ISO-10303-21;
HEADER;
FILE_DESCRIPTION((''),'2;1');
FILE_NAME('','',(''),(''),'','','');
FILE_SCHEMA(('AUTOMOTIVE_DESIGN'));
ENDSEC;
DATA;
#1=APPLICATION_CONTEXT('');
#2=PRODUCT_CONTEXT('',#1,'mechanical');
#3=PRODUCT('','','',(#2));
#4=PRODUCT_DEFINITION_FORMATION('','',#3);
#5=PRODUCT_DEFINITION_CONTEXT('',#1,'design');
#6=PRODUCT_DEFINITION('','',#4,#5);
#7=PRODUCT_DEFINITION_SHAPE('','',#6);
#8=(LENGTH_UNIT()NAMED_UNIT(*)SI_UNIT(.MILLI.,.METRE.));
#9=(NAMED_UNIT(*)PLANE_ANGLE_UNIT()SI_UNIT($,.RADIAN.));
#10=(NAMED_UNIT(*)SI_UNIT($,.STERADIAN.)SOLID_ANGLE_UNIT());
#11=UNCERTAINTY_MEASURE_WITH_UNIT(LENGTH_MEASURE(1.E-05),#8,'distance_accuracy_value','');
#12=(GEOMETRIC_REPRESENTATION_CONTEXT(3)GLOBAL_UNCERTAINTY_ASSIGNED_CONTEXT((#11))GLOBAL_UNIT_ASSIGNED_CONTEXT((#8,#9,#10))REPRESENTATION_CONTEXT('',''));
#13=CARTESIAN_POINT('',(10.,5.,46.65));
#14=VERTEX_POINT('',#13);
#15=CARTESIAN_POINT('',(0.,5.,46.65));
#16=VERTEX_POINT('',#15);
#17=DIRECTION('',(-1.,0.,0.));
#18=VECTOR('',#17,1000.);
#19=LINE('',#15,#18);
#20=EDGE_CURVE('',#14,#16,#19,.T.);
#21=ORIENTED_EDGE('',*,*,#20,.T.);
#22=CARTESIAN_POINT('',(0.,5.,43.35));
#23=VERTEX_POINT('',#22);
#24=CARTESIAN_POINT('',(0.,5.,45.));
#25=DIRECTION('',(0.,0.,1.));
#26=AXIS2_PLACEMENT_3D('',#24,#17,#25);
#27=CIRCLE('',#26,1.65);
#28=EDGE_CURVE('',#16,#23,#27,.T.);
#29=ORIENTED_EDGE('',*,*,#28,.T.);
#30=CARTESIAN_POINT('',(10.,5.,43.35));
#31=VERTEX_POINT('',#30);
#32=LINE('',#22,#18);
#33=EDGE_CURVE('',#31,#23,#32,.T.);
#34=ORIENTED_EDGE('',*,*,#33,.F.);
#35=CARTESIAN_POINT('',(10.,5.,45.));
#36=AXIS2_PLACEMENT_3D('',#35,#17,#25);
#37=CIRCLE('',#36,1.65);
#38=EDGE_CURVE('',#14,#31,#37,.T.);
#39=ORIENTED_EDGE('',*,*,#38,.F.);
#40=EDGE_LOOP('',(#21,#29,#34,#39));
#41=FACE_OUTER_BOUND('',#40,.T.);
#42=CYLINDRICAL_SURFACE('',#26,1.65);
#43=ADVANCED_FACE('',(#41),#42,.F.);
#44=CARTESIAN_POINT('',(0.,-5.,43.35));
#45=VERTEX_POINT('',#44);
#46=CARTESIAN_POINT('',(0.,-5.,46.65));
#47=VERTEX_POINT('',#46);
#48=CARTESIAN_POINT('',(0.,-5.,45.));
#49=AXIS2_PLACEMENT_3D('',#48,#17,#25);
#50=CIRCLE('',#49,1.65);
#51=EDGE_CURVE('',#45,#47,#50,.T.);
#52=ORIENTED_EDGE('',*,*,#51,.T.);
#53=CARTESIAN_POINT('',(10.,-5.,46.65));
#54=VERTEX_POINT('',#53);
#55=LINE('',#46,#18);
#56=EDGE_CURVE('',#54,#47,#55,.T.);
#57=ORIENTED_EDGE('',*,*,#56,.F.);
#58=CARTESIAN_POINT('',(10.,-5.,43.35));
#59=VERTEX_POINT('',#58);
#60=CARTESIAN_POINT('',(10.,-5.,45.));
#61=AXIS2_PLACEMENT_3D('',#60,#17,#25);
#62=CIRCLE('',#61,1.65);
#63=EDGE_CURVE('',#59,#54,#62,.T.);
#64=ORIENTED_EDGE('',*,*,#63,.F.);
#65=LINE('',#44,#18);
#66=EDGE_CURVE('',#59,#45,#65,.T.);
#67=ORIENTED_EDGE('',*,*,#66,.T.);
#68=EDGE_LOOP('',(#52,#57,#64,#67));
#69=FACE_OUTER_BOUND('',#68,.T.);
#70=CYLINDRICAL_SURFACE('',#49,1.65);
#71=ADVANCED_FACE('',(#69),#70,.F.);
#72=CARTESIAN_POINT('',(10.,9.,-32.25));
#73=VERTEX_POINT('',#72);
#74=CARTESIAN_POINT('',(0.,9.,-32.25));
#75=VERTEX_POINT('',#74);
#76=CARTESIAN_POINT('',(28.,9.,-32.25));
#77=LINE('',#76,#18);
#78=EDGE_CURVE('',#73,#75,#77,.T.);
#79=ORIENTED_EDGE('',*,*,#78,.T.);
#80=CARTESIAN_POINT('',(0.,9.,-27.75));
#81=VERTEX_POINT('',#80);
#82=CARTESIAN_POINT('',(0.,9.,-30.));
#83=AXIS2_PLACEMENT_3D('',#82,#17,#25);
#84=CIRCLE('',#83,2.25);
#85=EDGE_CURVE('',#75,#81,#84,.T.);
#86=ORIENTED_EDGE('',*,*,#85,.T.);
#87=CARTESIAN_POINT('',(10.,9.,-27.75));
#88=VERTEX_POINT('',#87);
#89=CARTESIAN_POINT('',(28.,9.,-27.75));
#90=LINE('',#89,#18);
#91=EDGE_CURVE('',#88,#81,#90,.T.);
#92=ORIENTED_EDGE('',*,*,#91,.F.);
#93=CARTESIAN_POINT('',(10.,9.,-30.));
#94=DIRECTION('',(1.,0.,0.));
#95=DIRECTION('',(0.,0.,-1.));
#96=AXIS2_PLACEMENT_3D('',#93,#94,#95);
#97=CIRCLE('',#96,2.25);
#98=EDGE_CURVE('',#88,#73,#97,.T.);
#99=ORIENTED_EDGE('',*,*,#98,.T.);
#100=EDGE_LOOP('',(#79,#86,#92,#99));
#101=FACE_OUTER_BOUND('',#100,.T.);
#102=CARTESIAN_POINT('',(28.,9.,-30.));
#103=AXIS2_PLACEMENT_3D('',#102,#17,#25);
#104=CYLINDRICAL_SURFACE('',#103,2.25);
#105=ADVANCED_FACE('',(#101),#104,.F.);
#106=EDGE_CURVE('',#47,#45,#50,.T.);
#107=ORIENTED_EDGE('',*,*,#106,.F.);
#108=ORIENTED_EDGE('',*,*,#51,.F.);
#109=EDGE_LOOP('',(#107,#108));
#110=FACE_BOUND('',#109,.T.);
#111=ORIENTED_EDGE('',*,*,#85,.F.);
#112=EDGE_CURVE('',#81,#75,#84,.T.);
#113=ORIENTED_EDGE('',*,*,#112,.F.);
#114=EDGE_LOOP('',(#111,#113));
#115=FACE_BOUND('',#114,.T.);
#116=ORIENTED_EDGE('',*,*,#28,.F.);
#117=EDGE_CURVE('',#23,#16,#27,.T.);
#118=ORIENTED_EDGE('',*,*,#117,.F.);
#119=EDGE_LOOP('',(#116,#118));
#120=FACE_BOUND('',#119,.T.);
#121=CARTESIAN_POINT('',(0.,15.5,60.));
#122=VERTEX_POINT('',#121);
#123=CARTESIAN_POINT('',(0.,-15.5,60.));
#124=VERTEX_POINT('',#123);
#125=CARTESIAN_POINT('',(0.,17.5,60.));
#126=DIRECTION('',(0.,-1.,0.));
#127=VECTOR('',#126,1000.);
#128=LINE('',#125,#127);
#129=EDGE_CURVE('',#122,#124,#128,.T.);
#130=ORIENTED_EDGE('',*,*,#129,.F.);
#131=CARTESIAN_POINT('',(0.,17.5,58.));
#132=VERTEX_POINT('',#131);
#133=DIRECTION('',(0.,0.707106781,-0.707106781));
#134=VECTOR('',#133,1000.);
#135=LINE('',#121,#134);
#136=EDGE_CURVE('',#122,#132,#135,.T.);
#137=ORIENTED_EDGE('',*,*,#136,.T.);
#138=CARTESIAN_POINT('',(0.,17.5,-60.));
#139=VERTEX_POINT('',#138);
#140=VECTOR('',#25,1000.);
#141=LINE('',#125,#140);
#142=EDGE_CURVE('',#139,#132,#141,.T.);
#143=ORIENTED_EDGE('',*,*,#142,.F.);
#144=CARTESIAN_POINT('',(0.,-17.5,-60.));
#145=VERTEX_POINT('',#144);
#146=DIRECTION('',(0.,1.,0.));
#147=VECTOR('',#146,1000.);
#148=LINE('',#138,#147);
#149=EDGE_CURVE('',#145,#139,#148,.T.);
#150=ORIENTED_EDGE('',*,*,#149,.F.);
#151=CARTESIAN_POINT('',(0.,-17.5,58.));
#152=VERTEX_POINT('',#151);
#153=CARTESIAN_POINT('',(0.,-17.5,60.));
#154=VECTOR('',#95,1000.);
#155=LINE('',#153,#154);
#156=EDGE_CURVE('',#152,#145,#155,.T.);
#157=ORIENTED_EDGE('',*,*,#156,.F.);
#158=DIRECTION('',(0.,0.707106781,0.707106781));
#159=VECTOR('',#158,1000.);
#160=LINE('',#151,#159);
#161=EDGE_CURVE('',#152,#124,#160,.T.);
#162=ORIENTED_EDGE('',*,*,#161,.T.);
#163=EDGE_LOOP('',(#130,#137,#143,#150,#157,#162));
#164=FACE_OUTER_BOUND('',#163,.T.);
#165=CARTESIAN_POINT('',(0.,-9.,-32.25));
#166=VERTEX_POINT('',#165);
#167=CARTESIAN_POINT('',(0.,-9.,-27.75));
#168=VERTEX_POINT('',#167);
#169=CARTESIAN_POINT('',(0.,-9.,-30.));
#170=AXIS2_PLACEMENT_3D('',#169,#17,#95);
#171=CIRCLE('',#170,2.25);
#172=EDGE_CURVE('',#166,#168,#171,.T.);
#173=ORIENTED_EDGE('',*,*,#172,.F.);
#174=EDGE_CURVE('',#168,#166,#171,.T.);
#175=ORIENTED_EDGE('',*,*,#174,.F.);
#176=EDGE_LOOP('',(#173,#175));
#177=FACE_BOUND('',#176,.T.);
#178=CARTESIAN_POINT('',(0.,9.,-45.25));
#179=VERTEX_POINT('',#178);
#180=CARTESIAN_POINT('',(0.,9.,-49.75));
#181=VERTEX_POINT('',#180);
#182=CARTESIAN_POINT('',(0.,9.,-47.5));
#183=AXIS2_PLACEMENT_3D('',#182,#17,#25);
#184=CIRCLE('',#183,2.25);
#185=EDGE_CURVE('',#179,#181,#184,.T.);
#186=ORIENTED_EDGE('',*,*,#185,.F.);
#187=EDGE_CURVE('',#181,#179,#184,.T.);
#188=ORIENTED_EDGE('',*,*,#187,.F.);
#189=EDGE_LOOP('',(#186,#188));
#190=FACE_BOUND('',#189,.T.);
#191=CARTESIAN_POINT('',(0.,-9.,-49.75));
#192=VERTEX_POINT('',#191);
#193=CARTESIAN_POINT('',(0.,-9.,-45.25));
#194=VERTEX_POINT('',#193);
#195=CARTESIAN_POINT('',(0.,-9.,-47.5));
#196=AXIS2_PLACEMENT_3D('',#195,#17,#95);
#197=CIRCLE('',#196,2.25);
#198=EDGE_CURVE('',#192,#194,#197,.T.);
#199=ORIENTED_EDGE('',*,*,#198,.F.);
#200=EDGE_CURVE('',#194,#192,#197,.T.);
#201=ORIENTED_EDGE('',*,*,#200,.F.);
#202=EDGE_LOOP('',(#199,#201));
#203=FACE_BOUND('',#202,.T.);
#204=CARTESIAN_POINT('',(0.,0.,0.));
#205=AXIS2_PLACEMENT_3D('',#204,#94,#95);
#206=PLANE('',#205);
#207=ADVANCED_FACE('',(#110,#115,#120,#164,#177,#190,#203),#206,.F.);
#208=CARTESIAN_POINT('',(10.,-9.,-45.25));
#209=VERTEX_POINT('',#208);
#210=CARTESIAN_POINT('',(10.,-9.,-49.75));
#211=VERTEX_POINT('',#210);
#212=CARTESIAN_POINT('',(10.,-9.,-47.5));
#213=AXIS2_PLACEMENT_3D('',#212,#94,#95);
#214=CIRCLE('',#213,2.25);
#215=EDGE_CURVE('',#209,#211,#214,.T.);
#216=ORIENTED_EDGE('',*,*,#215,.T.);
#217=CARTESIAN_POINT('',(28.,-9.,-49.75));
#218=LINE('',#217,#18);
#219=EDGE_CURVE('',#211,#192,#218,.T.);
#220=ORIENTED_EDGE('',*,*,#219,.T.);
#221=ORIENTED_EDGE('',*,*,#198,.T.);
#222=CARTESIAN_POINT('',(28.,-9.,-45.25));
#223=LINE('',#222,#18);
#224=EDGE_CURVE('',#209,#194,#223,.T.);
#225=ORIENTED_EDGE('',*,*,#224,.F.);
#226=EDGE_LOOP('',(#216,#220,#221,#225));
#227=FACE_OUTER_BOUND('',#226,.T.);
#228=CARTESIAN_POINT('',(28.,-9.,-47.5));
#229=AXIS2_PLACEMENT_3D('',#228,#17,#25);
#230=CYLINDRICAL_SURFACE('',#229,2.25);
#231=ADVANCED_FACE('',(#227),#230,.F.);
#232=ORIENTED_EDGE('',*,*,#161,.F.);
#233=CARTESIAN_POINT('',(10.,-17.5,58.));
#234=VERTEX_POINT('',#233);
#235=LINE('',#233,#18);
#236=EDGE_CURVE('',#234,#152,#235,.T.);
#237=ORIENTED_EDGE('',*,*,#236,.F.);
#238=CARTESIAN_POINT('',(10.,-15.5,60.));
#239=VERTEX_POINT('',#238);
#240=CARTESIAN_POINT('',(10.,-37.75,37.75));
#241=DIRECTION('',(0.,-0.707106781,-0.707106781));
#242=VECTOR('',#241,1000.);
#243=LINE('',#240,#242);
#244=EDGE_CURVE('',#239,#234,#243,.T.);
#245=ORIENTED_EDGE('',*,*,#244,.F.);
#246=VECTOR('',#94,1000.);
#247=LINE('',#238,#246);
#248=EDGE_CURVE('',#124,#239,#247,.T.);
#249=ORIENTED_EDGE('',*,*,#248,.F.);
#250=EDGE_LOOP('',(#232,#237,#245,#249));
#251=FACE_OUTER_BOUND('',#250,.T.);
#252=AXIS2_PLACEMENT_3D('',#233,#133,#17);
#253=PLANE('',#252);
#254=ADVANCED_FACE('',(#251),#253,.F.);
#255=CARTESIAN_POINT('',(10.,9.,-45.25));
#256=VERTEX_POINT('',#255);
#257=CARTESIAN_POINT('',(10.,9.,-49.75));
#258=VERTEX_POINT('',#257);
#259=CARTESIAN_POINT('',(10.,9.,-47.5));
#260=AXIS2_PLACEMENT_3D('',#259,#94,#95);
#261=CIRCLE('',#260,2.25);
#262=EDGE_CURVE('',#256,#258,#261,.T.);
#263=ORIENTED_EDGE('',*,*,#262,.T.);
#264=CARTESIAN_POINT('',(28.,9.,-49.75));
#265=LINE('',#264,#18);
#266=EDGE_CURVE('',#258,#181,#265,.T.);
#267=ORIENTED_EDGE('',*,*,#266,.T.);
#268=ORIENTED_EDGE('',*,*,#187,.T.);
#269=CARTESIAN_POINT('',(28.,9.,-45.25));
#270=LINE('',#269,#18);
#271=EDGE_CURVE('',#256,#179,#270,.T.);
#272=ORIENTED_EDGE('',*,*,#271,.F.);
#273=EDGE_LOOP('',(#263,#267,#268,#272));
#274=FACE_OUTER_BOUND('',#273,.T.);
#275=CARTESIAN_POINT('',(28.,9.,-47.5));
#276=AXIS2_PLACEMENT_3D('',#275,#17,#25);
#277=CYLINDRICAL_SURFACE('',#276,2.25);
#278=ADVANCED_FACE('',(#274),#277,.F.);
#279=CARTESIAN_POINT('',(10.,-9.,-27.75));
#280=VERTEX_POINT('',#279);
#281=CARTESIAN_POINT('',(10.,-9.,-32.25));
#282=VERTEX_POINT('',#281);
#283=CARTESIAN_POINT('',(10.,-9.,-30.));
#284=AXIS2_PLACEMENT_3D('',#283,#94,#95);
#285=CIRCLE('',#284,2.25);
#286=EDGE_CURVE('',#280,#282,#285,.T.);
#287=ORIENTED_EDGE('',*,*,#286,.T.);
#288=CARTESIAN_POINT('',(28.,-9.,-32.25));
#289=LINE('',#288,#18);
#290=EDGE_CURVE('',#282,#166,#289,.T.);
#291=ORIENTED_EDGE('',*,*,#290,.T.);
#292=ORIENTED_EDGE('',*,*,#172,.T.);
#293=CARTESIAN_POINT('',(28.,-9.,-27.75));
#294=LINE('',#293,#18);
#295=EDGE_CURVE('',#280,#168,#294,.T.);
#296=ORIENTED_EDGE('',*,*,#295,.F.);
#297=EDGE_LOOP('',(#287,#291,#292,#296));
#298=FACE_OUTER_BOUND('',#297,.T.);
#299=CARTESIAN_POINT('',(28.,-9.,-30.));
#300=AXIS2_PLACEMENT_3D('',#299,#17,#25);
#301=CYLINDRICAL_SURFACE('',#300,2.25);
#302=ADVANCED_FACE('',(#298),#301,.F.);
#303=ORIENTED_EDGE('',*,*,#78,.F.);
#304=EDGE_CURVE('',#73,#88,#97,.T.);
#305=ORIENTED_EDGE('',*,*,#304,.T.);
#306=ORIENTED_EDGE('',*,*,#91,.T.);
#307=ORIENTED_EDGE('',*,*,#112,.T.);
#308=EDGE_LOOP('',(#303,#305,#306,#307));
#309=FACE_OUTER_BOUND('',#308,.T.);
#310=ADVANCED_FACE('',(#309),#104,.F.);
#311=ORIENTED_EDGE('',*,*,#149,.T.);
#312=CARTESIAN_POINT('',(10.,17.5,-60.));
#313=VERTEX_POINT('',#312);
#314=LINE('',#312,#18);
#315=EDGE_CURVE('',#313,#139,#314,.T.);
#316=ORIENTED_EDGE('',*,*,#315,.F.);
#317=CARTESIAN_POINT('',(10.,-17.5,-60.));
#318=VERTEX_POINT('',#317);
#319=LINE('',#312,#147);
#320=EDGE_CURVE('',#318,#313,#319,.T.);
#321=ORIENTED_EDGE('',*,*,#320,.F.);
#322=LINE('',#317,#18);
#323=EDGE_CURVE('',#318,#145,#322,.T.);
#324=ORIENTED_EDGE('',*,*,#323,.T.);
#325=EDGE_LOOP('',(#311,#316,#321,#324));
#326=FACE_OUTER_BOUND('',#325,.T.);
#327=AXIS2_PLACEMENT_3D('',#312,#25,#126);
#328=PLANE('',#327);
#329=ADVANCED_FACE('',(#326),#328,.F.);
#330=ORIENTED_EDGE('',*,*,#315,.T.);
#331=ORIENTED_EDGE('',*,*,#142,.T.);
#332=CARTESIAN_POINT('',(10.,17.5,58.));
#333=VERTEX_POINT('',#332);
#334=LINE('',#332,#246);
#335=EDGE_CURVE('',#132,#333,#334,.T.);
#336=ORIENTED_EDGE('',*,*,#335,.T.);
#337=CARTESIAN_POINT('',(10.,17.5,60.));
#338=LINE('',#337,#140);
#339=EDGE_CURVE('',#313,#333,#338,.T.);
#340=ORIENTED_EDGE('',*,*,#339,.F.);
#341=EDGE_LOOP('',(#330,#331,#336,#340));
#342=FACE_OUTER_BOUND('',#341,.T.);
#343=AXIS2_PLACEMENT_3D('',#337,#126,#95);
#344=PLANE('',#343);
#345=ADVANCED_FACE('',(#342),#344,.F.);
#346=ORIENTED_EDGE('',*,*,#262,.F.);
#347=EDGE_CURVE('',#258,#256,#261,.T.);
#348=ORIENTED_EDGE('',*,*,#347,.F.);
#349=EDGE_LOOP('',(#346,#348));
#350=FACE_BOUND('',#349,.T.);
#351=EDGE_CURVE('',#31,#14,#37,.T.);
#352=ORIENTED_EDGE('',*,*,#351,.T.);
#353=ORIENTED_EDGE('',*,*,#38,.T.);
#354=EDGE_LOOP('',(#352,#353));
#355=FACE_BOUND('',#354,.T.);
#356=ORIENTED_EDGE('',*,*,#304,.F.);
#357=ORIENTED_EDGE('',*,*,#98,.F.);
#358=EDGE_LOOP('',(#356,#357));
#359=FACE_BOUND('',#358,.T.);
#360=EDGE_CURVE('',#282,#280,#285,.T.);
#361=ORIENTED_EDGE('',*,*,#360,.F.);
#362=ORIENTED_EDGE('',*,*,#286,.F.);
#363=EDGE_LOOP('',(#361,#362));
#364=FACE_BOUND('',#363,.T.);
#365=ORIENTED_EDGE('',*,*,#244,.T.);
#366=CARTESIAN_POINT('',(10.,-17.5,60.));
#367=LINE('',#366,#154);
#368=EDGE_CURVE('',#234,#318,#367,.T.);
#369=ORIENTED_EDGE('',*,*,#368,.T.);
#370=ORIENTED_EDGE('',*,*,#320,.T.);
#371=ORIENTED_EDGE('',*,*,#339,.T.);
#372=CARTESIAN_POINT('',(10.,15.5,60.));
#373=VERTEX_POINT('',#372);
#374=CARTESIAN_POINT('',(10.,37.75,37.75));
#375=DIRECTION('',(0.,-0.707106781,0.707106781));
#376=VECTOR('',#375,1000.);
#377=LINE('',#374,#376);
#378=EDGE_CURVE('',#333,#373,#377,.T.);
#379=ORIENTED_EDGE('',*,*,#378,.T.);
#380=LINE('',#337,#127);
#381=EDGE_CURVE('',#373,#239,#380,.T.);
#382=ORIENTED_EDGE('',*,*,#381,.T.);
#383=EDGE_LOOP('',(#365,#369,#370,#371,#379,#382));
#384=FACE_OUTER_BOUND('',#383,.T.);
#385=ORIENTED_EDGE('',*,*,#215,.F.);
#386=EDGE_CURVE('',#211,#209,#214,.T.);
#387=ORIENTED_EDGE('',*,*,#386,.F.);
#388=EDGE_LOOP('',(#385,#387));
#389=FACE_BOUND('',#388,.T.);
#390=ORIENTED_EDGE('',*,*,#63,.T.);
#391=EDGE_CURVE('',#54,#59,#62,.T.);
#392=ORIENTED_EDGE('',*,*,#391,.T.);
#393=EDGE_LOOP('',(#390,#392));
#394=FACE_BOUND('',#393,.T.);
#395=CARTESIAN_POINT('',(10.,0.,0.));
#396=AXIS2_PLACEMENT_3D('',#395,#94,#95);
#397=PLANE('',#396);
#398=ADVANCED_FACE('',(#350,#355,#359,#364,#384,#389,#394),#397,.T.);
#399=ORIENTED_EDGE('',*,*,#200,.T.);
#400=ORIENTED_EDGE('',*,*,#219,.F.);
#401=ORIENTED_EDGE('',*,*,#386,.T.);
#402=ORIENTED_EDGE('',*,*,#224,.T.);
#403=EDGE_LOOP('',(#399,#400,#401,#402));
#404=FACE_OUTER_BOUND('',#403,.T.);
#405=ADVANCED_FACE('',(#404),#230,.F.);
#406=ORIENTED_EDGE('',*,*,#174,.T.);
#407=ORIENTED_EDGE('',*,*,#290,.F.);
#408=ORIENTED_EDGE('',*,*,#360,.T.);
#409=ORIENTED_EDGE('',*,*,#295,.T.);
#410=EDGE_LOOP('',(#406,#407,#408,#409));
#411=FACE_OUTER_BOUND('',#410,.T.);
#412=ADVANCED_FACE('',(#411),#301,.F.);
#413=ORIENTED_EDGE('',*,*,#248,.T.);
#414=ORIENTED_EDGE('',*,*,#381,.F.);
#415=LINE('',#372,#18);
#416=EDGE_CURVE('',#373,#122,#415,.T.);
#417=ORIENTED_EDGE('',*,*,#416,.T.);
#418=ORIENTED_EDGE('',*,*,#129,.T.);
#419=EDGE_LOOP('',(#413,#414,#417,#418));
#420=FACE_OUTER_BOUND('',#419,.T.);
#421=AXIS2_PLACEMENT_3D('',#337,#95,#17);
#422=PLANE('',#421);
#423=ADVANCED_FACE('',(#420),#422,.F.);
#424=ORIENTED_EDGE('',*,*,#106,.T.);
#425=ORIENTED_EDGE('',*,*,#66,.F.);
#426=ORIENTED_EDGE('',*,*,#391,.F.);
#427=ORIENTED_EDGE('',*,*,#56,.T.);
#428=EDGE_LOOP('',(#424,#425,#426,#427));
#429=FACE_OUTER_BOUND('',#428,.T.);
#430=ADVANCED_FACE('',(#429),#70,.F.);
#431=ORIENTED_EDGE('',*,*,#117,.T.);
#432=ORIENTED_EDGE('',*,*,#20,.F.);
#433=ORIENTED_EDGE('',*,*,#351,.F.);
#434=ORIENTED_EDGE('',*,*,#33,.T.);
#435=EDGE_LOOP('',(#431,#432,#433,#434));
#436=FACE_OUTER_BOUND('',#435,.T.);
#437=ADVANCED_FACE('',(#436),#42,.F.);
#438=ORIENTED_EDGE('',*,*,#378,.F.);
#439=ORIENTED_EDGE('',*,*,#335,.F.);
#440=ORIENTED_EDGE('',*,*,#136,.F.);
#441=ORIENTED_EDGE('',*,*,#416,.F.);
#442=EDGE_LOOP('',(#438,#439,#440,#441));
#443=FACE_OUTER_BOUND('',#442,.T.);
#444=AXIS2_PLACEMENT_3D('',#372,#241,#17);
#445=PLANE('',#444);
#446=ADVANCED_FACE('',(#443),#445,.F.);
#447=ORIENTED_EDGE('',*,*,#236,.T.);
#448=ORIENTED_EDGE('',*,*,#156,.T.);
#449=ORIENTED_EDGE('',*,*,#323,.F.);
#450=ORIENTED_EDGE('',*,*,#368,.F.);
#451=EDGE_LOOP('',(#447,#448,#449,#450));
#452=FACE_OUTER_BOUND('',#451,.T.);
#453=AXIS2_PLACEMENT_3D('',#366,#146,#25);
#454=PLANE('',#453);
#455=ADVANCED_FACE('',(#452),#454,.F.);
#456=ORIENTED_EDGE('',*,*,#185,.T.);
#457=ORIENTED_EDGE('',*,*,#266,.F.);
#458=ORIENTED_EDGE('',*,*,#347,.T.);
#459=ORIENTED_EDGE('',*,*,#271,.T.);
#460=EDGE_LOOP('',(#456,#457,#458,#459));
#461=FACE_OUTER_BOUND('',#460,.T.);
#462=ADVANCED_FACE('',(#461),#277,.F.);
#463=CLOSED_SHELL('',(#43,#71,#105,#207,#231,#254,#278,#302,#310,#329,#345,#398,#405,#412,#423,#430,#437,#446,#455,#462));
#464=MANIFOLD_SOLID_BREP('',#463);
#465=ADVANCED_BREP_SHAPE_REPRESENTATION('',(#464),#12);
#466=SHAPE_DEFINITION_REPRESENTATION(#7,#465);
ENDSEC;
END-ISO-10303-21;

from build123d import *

# Parameters (mm, degrees)
SKETCH_1_W             = 120
SKETCH_1_H             = 35
EXTRUDE_1_DEPTH        = 10
HOLE_WIZARD_M4_1_D     = 3.3
SKETCH_5_R             = 2.25
CUT_EXTRUDE_1_DEPTH    = 28
CHAMFER_1_SIZE         = 2
PATTERN_LINEAR_1_COUNT = 2
PATTERN_LINEAR_1_PITCH = 17.5


with BuildPart() as part:
    # 草图1 → 凸台-拉伸1 (new body)
    with BuildSketch(Plane(origin=(0, 0, 0), x_dir=(0, 0, -1), z_dir=(1, 0, 0))):
        Rectangle(SKETCH_1_W, SKETCH_1_H)
    extrude(amount=EXTRUDE_1_DEPTH)

    # M4 螺纹孔1 (through all)
    with Locations(Plane.ZY):
        with Locations((45, 5), (45, -5)):
            Hole(HOLE_WIZARD_M4_1_D / 2)

    # 草图5 → 切除-拉伸1 (cut)
    with BuildSketch(Plane.ZY):
        with Locations((-47.5, 9)):
            Circle(SKETCH_5_R)
        with Locations(Location((-47.5, -9, 0), (0, 0, 180))):
            Circle(SKETCH_5_R)
    cut_extrude_1 = extrude(amount=-CUT_EXTRUDE_1_DEPTH, mode=Mode.SUBTRACT)

    # 倒角1
    chamfer_1_edges = [part.edges().sort_by_distance(p)[0] for p in [
        (5, -17.5, 60),
        (5, 17.5, 60),
    ]]
    chamfer(chamfer_1_edges, length=CHAMFER_1_SIZE)

    # 阵列(线性)1: 切除-拉伸1 ×2
    with Locations(*[(0, 0, i * PATTERN_LINEAR_1_PITCH) for i in range(1, PATTERN_LINEAR_1_COUNT)]):
        add(cut_extrude_1, mode=Mode.SUBTRACT)


solid = part.part
